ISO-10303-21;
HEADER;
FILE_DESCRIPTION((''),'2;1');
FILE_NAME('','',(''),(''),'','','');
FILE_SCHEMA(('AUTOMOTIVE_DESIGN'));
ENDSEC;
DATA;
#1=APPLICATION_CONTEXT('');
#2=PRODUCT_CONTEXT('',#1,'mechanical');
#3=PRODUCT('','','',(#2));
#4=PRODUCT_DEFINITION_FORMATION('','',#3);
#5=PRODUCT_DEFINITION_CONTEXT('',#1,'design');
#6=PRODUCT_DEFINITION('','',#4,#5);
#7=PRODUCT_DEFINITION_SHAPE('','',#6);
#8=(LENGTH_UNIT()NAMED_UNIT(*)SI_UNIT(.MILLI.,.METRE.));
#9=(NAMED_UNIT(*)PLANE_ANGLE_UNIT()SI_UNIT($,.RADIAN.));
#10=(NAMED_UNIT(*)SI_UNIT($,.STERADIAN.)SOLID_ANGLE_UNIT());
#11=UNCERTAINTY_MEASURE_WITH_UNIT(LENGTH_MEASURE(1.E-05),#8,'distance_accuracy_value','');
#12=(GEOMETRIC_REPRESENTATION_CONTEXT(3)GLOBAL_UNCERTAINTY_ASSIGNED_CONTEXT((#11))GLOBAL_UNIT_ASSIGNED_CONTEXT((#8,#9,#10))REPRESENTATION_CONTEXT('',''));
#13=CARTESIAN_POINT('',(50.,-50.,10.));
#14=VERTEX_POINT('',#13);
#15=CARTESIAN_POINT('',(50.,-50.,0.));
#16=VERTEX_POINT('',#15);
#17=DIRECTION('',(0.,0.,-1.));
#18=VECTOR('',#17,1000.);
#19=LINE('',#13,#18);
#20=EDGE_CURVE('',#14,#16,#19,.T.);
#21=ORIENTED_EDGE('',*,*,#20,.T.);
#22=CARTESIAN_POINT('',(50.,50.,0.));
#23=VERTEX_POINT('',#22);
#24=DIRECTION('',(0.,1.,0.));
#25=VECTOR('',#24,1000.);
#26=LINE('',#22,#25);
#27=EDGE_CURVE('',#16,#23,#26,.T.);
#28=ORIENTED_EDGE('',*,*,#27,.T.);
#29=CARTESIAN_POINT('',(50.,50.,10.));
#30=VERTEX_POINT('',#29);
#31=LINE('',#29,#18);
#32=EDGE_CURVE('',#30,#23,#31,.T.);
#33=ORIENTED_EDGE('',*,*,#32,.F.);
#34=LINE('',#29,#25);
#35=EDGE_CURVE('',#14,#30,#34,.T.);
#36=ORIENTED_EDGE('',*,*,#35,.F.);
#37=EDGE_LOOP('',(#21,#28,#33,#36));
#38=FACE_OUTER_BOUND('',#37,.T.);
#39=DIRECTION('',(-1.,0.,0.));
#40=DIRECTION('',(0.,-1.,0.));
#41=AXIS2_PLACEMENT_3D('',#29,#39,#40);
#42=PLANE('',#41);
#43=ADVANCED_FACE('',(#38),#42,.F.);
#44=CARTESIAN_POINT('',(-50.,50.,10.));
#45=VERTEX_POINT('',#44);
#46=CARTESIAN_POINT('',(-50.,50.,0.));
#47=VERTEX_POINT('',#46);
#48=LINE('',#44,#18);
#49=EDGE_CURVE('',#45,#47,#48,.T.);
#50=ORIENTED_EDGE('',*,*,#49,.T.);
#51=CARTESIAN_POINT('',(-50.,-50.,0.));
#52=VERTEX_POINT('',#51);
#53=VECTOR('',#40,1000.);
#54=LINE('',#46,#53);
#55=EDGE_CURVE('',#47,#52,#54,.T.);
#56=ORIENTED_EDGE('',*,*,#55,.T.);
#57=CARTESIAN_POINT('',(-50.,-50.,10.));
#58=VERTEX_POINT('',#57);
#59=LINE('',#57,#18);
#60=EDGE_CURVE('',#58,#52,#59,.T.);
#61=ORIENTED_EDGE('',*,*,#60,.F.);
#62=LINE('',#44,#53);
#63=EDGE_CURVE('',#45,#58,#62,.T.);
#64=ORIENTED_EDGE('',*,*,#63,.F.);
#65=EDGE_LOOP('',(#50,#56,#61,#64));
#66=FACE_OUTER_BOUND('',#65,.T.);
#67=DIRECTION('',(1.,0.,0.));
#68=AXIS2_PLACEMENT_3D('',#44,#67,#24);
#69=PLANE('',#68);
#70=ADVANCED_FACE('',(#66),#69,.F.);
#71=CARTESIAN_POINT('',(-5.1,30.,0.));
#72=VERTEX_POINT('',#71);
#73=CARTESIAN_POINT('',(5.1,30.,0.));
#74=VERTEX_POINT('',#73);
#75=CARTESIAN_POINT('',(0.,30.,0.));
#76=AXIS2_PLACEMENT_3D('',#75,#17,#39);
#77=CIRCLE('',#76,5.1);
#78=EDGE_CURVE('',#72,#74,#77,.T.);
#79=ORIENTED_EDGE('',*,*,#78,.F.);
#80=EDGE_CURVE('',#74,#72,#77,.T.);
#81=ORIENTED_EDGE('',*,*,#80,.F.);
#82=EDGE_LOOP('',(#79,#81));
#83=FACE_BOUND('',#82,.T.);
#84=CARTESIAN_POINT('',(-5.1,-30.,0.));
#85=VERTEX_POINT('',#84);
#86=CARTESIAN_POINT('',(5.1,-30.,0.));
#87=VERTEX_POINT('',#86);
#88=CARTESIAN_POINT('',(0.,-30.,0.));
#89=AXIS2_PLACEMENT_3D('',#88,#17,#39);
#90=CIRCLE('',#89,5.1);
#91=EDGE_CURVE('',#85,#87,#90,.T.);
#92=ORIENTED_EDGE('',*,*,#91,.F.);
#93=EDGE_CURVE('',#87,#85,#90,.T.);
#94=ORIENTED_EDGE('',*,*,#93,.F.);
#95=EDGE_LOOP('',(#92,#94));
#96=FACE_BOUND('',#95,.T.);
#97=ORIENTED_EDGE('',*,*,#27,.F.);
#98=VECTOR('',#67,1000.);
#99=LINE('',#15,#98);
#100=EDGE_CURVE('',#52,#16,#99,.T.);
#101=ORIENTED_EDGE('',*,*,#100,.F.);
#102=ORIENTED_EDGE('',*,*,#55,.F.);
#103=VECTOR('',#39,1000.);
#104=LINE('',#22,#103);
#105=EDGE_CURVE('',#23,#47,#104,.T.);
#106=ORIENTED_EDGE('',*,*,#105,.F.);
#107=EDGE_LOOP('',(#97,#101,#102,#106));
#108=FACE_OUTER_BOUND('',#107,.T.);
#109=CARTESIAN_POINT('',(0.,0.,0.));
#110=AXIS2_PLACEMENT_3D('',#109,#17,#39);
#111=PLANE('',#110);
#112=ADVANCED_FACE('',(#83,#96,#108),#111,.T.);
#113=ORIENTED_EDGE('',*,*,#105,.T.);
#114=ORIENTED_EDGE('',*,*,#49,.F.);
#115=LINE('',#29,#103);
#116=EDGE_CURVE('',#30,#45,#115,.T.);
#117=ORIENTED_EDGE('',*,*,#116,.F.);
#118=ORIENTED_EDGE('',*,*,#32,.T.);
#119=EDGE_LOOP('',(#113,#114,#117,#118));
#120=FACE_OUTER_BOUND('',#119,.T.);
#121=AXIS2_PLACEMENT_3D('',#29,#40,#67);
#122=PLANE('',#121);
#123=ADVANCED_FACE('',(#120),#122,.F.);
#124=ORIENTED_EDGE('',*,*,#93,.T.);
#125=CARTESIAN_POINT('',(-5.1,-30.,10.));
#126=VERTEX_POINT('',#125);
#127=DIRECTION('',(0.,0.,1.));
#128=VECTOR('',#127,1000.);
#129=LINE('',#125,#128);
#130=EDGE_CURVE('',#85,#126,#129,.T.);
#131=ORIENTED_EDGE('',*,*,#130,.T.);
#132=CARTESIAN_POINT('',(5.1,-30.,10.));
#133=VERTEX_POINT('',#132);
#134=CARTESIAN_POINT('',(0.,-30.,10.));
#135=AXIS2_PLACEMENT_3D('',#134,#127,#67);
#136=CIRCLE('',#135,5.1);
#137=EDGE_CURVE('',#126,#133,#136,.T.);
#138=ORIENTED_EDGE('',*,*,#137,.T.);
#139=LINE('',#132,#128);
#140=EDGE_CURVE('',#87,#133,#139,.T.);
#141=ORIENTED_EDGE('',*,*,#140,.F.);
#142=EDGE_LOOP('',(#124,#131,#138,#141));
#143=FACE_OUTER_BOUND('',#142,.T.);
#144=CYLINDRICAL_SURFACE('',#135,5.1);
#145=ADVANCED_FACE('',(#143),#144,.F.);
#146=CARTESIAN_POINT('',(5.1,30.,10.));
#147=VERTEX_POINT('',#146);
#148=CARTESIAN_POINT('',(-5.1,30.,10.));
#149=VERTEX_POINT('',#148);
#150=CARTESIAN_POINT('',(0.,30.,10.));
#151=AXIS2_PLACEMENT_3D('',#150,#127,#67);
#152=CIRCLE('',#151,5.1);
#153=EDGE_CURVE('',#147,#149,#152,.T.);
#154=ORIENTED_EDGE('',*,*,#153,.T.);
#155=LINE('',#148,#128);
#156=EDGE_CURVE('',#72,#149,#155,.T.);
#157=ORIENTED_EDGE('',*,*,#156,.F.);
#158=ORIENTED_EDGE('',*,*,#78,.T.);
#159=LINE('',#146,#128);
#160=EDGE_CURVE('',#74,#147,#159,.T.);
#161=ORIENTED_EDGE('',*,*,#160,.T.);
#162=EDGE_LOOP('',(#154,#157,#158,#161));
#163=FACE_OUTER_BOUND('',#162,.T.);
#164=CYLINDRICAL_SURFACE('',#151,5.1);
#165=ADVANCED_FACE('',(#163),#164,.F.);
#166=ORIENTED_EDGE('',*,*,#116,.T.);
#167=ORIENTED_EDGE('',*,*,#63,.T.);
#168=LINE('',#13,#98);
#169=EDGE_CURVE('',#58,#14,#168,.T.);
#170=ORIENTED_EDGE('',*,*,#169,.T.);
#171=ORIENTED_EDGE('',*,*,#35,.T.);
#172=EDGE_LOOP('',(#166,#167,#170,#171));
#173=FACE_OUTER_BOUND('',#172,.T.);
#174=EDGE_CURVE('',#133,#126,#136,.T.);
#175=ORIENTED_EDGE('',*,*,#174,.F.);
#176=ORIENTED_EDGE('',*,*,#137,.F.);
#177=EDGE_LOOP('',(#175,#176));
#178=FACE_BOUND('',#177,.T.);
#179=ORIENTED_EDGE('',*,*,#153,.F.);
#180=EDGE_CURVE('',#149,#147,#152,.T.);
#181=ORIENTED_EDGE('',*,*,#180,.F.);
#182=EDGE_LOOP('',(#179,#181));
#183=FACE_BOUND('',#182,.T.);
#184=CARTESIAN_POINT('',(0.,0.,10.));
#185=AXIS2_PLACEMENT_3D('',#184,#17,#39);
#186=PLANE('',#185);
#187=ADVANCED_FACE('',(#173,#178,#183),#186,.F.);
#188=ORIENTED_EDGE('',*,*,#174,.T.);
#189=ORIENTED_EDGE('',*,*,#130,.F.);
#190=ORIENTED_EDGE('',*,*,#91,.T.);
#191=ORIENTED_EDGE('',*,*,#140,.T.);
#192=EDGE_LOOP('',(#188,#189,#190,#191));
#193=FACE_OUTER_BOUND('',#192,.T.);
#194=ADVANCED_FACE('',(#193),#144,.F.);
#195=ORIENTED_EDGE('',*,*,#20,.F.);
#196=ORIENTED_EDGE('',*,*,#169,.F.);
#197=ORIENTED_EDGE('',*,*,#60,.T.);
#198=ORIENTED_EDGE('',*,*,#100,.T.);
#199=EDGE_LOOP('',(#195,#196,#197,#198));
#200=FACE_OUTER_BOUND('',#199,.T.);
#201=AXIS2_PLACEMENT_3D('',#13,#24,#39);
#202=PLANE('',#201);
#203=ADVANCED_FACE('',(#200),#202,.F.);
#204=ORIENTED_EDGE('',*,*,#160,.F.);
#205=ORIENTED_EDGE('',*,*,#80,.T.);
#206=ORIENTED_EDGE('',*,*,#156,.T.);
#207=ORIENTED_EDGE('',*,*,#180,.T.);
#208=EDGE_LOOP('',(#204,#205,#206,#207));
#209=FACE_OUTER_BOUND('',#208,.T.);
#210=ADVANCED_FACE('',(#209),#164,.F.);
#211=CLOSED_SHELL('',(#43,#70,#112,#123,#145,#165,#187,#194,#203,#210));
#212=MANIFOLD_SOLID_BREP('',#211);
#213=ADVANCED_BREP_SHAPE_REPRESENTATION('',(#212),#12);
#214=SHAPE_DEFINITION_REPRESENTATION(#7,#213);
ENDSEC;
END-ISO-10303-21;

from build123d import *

# Parameters (mm, degrees)
SKETCH1_W              = 100
SKETCH1_H              = 100
BOSS_EXTRUDE1_DEPTH    = 10
M12_TAPPED_HOLE1_D     = 10.2
M12_TAPPED_HOLE1_DEPTH = 29.25
M12_TAPPED_HOLE1_TIP   = 3.064389157


with BuildPart() as part:
    # Sketch1 → Boss-Extrude1 (new body)
    with BuildSketch(Plane.XY):
        Rectangle(SKETCH1_W, SKETCH1_H)
    extrude(amount=BOSS_EXTRUDE1_DEPTH)

    # M12 Tapped Hole1
    with Locations(Plane.XY.offset(10)):
        with Locations((0, 30), (0, -30)):
            Hole(M12_TAPPED_HOLE1_D / 2, depth=M12_TAPPED_HOLE1_DEPTH)
            with Locations((0, 0, -(M12_TAPPED_HOLE1_DEPTH + M12_TAPPED_HOLE1_TIP / 2))):  # 118° drill point
                Cone(0, M12_TAPPED_HOLE1_D / 2, M12_TAPPED_HOLE1_TIP, mode=Mode.SUBTRACT)


solid = part.part
